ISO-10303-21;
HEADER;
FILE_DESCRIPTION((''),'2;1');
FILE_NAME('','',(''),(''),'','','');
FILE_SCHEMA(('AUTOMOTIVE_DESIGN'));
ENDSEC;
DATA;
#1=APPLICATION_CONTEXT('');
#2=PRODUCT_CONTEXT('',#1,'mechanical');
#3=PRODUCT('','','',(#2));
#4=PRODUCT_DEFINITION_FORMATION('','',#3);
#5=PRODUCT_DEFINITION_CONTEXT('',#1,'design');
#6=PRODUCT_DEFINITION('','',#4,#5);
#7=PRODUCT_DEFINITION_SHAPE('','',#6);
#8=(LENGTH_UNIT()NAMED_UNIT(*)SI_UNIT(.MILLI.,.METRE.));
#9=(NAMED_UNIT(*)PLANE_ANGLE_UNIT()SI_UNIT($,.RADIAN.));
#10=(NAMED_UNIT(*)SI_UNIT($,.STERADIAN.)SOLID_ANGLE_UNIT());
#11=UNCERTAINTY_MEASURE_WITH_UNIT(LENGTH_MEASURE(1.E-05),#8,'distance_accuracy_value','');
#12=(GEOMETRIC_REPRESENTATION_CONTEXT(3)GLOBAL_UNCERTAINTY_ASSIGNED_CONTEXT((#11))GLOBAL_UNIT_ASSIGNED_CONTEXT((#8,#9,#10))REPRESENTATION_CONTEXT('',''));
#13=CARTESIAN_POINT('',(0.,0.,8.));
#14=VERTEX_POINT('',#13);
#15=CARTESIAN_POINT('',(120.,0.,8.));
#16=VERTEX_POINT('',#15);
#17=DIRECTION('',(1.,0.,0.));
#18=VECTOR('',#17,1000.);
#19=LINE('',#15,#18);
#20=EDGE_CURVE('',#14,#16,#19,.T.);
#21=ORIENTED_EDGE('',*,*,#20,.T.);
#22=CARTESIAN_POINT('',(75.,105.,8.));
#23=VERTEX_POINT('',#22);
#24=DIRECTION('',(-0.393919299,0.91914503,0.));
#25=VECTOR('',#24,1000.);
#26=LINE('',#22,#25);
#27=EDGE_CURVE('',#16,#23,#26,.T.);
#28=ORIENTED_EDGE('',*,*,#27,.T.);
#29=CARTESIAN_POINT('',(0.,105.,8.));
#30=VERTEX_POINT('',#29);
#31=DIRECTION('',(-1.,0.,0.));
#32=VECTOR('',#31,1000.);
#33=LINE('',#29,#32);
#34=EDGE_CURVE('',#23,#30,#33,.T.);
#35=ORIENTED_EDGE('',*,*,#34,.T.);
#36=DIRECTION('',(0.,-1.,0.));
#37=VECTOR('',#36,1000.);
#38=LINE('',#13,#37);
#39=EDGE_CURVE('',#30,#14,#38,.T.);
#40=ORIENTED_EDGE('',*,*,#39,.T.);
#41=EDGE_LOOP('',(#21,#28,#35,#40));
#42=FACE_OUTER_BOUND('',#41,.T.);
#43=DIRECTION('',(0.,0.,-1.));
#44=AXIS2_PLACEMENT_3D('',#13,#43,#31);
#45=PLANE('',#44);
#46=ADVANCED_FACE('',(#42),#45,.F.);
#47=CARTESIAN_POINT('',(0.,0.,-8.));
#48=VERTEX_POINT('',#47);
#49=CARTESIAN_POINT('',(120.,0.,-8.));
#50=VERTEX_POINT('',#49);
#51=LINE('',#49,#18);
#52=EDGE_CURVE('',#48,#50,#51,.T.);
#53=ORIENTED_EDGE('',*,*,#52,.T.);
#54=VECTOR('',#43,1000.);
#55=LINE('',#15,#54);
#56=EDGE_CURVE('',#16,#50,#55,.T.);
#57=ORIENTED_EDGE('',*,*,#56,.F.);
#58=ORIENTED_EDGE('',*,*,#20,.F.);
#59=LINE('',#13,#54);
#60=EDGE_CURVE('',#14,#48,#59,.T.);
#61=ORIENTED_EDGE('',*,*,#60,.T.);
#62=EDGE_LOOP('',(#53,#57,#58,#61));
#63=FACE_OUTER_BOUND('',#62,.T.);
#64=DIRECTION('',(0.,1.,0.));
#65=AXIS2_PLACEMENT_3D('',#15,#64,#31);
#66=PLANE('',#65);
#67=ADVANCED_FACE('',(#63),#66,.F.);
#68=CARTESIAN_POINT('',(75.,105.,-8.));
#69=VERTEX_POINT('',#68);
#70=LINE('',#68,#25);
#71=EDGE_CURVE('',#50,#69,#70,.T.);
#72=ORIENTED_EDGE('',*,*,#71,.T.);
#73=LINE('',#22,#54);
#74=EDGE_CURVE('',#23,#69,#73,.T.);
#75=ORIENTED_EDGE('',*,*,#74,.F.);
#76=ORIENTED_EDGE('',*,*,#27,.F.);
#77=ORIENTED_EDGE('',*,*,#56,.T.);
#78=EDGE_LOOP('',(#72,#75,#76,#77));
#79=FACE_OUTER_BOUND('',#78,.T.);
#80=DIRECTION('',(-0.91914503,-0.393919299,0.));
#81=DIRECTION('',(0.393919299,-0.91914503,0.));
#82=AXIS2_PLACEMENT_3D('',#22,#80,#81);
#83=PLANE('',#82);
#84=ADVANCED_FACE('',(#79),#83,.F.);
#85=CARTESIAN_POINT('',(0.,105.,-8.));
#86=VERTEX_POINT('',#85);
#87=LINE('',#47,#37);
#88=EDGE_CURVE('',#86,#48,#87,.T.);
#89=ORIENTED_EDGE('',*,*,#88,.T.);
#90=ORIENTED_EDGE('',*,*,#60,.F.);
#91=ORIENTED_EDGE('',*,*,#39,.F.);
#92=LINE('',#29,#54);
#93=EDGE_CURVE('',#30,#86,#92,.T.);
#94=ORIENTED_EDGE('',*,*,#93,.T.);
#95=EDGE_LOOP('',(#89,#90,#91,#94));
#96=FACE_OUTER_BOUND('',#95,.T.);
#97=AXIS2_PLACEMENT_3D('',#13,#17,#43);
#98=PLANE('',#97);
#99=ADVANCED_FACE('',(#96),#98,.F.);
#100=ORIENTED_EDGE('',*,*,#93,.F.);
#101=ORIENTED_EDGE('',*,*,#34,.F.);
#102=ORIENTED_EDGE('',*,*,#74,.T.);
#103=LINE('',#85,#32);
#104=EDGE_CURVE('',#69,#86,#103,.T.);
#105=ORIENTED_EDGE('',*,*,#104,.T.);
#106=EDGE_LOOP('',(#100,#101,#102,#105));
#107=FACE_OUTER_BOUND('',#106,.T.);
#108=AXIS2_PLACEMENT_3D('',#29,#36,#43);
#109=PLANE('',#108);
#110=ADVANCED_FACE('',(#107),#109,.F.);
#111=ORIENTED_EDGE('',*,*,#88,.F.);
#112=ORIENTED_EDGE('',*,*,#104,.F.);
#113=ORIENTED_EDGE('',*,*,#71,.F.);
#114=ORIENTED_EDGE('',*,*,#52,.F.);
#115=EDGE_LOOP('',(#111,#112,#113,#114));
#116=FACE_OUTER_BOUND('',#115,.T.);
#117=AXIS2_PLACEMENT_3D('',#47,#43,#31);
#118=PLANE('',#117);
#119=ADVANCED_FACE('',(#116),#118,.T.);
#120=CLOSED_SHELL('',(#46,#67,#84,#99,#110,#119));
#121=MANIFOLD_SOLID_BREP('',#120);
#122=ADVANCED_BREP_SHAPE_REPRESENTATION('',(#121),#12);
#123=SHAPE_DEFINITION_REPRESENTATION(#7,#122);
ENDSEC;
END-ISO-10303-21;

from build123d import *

# Parameters (mm, degrees)
BOSS_EXTRUDE1_DEPTH = 8


with BuildPart() as part:
    # Sketch1 → Boss-Extrude1 (new, symmetric)
    with BuildSketch(Plane.XY):
        Polygon((0, 0), (0, 105), (75, 105), (120, 0), align=None)
    extrude(amount=BOSS_EXTRUDE1_DEPTH, both=True)


solid = part.part
